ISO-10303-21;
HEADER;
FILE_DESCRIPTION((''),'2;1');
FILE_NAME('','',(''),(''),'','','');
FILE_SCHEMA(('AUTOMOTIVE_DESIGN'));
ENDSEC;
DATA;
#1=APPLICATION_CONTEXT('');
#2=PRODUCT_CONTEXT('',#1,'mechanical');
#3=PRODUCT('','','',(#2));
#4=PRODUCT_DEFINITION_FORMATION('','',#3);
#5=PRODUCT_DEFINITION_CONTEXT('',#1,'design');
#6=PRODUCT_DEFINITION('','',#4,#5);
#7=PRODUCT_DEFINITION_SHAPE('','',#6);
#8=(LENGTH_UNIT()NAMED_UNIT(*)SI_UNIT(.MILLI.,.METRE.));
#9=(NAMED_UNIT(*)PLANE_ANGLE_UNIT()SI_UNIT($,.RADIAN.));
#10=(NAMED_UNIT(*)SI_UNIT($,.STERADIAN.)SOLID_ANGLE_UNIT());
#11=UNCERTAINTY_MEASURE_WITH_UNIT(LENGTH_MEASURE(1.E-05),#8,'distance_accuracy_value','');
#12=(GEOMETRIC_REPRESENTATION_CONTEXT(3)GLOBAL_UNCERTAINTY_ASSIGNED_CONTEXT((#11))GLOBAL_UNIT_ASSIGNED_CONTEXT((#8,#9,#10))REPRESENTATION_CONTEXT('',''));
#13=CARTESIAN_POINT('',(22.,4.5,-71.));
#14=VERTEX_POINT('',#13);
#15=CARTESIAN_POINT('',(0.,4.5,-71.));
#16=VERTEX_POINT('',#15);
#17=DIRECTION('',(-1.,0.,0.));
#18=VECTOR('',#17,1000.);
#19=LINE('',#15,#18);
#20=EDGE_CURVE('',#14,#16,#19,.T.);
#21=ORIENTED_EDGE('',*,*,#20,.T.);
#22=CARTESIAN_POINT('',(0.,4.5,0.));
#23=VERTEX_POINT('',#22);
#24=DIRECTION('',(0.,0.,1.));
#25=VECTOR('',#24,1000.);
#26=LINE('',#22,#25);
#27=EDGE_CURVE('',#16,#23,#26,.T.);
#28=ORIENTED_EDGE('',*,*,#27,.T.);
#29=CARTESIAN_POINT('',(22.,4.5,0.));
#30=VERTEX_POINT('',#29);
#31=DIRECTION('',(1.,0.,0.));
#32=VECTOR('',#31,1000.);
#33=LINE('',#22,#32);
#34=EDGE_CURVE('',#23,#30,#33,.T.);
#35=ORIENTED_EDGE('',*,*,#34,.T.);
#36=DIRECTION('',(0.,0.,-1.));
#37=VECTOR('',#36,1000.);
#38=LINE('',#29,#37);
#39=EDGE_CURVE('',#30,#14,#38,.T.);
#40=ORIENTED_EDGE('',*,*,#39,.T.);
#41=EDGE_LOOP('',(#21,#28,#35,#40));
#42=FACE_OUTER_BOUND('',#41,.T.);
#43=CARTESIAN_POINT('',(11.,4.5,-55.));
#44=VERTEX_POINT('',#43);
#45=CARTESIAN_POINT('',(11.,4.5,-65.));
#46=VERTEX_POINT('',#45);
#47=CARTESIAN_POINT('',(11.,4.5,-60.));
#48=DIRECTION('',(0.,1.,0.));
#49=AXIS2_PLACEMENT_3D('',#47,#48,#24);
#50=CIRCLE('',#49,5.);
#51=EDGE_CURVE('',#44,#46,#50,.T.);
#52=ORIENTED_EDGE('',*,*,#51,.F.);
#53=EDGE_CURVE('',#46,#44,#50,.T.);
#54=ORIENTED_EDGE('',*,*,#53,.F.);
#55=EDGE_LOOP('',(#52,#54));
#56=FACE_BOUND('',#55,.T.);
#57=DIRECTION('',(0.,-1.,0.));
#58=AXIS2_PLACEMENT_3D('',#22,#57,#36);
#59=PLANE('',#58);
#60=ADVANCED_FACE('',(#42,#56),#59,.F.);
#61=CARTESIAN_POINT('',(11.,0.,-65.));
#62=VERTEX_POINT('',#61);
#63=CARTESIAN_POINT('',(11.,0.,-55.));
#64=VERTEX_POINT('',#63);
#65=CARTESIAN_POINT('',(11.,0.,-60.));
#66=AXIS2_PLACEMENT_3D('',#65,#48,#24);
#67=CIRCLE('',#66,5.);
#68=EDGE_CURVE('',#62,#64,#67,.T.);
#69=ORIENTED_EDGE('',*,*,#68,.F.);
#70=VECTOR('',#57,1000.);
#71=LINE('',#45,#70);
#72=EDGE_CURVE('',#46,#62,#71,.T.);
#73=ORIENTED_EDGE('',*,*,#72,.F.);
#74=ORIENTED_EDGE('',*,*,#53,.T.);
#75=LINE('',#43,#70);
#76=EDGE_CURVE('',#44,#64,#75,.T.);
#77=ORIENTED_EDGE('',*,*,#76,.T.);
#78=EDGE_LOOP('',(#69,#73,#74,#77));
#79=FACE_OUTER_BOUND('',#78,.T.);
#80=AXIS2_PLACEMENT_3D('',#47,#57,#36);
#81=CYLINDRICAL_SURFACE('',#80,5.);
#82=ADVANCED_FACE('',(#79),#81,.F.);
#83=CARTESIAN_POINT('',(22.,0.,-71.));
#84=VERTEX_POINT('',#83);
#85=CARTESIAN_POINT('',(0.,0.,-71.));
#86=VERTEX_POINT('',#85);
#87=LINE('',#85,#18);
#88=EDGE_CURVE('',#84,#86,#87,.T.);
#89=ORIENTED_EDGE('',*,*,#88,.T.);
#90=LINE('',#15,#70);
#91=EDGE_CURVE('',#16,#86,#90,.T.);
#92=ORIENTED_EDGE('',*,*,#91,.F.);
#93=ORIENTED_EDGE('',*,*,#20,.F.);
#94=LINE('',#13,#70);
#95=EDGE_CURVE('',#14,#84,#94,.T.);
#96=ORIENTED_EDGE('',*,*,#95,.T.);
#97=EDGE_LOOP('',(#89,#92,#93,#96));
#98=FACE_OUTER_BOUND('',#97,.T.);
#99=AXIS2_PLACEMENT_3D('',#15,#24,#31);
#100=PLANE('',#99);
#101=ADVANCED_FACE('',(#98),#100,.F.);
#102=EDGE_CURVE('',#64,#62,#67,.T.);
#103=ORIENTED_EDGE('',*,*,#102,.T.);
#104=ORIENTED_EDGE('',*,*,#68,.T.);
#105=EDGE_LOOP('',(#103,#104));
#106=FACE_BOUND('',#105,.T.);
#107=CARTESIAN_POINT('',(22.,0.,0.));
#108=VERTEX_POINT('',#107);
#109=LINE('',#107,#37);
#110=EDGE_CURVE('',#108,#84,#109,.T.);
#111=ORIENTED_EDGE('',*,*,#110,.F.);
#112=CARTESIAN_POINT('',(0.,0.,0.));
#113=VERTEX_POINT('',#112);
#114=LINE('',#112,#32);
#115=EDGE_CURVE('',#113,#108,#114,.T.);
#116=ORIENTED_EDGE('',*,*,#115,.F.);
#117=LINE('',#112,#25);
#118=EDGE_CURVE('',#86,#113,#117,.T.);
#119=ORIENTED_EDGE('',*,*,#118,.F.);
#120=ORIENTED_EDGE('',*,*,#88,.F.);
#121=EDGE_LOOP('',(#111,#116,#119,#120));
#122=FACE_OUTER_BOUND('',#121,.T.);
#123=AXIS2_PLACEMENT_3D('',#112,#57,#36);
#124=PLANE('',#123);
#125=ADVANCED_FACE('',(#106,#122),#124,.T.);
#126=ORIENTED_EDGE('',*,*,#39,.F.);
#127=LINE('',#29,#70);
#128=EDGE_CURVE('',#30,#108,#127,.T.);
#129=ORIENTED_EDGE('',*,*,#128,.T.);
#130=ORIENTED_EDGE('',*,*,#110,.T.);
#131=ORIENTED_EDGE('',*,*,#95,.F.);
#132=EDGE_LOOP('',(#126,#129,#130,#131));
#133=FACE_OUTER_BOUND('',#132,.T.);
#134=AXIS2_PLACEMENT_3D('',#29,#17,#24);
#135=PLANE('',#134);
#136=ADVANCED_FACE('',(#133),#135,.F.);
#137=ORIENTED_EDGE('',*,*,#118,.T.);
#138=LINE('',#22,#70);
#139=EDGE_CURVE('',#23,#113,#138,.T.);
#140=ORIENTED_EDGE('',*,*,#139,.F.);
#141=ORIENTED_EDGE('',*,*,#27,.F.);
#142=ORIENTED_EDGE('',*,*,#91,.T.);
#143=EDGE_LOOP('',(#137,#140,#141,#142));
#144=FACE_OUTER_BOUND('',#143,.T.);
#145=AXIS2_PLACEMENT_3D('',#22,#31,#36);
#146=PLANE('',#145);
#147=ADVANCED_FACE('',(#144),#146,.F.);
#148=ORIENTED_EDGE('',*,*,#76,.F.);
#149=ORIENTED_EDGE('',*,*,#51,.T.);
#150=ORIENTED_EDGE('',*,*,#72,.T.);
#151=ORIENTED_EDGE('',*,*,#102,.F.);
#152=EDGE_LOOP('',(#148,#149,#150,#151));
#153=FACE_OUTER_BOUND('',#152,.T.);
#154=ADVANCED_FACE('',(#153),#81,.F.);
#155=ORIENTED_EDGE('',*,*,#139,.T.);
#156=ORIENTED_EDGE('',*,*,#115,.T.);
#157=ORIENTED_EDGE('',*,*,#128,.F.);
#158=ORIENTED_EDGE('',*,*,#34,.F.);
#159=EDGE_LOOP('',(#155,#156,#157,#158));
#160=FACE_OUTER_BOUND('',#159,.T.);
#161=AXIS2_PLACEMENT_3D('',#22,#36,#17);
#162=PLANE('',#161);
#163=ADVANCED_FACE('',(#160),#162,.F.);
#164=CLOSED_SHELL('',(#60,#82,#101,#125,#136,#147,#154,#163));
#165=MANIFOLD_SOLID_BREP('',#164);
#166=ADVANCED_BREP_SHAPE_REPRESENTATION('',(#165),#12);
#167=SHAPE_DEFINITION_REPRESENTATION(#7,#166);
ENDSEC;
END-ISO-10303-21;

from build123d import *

# Parameters (mm, degrees)
SKETCH1_W           = 22
SKETCH1_H           = 71
SKETCH1_R           = 5
BOSS_EXTRUDE1_DEPTH = 4.5


with BuildPart() as part:
    # Sketch1 → Boss-Extrude1 (new body)
    with BuildSketch(Plane(origin=(0, 0, 0), x_dir=(1, 0, 0), z_dir=(0, 1, 0))):
        with Locations((11, 35.5)):
            Rectangle(SKETCH1_W, SKETCH1_H)
        with Locations(Location((11, 60, 0), (0, 0, 270))):
            Circle(SKETCH1_R, mode=Mode.SUBTRACT)
    extrude(amount=BOSS_EXTRUDE1_DEPTH)


solid = part.part
